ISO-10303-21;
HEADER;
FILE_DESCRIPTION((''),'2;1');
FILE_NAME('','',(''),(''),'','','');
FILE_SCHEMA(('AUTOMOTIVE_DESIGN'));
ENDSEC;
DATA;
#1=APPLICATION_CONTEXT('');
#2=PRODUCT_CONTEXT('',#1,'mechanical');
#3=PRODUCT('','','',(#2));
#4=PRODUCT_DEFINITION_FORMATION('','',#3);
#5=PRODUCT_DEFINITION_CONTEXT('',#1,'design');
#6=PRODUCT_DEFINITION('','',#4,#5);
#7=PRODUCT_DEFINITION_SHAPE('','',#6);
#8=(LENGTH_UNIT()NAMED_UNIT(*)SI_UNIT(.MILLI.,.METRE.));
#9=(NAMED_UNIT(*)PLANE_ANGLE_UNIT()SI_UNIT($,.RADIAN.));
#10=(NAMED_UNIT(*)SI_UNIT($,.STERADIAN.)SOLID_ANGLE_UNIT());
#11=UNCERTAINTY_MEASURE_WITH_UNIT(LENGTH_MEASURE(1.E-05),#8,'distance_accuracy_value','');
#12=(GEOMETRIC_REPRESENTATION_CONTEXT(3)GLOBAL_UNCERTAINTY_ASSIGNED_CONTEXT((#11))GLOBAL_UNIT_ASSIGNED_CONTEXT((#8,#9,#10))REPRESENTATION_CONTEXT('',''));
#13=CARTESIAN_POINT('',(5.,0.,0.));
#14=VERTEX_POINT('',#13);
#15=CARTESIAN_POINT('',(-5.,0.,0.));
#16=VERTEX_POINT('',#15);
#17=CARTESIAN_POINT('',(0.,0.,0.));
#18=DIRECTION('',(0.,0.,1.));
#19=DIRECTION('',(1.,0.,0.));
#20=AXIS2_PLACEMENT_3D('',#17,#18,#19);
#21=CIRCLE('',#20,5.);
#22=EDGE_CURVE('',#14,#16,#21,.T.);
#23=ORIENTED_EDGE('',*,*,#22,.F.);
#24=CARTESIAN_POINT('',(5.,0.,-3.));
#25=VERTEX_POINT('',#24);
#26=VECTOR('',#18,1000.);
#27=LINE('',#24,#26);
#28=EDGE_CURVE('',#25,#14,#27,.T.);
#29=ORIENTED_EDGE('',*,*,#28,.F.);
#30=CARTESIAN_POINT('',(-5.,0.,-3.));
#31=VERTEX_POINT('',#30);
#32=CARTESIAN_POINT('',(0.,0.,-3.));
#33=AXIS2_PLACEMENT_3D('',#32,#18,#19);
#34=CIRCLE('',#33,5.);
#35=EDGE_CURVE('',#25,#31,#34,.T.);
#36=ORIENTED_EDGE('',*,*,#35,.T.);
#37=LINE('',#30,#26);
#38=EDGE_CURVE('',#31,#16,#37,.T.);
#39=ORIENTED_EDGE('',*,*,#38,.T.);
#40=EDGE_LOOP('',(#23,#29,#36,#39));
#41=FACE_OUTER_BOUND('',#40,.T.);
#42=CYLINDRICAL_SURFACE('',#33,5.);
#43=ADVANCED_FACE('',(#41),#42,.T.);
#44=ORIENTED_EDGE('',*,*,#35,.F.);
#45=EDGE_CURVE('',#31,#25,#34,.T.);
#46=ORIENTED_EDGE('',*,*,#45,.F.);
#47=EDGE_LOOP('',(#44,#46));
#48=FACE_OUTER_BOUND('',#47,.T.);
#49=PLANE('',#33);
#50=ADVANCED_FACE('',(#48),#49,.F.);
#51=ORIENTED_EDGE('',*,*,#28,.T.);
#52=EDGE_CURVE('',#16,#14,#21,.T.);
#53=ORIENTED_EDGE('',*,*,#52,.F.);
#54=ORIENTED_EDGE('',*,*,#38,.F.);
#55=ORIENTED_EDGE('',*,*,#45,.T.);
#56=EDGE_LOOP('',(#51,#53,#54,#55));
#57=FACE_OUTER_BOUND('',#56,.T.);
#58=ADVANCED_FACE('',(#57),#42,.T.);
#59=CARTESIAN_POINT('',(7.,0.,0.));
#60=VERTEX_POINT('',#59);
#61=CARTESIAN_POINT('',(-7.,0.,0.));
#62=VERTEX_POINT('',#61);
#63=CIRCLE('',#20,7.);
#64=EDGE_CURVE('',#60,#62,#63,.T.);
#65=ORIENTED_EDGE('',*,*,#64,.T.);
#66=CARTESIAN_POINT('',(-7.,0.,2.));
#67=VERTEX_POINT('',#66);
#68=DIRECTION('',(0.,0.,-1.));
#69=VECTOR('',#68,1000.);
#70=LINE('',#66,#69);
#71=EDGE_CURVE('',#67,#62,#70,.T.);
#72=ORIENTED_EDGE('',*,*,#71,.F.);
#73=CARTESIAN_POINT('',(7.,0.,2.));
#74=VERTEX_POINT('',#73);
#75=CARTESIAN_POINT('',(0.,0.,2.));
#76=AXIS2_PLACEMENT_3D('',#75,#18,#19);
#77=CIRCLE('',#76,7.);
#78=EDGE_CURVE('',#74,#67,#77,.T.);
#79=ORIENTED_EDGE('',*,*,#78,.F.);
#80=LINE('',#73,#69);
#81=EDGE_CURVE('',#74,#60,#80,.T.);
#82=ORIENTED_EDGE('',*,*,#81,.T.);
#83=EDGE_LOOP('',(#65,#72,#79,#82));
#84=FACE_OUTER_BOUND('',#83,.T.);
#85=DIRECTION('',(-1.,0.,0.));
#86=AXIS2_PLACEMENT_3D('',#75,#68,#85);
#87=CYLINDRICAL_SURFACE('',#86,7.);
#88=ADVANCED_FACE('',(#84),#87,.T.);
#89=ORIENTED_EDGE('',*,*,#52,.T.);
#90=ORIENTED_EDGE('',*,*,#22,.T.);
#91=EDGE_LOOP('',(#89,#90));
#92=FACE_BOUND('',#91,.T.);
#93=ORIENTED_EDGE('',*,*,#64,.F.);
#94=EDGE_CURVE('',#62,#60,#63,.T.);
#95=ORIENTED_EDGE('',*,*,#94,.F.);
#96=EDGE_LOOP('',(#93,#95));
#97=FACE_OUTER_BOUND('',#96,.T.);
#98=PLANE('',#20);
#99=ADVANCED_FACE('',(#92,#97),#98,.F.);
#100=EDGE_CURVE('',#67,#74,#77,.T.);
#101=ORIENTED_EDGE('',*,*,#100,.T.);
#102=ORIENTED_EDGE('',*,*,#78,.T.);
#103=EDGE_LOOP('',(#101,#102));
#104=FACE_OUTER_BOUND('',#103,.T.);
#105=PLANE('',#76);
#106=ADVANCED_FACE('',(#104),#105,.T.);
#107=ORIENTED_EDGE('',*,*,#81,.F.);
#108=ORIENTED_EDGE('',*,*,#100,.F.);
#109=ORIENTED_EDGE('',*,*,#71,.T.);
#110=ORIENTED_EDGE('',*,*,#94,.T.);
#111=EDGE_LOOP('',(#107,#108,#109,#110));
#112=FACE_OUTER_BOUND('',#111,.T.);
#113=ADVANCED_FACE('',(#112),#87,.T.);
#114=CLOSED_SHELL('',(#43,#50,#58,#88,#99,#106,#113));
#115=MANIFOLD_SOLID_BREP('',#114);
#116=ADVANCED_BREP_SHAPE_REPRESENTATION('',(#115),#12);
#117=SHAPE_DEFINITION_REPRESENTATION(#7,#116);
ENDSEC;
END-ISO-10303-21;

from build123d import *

# Parameters (mm, degrees)
SKETCH_1_R      = 5
EXTRUDE_1_DEPTH = 3
SKETCH_2_R      = 7
EXTRUDE_2_DEPTH = 2


with BuildPart() as part:
    # 草图1 → 凸台-拉伸1 (new body)
    with BuildSketch(Plane.XY):
        Circle(SKETCH_1_R)
    extrude(amount=-EXTRUDE_1_DEPTH)

    # 草图2 → 凸台-拉伸2 (add)
    with BuildSketch(Plane.XY):
        Circle(SKETCH_2_R)
    extrude(amount=EXTRUDE_2_DEPTH)


solid = part.part
